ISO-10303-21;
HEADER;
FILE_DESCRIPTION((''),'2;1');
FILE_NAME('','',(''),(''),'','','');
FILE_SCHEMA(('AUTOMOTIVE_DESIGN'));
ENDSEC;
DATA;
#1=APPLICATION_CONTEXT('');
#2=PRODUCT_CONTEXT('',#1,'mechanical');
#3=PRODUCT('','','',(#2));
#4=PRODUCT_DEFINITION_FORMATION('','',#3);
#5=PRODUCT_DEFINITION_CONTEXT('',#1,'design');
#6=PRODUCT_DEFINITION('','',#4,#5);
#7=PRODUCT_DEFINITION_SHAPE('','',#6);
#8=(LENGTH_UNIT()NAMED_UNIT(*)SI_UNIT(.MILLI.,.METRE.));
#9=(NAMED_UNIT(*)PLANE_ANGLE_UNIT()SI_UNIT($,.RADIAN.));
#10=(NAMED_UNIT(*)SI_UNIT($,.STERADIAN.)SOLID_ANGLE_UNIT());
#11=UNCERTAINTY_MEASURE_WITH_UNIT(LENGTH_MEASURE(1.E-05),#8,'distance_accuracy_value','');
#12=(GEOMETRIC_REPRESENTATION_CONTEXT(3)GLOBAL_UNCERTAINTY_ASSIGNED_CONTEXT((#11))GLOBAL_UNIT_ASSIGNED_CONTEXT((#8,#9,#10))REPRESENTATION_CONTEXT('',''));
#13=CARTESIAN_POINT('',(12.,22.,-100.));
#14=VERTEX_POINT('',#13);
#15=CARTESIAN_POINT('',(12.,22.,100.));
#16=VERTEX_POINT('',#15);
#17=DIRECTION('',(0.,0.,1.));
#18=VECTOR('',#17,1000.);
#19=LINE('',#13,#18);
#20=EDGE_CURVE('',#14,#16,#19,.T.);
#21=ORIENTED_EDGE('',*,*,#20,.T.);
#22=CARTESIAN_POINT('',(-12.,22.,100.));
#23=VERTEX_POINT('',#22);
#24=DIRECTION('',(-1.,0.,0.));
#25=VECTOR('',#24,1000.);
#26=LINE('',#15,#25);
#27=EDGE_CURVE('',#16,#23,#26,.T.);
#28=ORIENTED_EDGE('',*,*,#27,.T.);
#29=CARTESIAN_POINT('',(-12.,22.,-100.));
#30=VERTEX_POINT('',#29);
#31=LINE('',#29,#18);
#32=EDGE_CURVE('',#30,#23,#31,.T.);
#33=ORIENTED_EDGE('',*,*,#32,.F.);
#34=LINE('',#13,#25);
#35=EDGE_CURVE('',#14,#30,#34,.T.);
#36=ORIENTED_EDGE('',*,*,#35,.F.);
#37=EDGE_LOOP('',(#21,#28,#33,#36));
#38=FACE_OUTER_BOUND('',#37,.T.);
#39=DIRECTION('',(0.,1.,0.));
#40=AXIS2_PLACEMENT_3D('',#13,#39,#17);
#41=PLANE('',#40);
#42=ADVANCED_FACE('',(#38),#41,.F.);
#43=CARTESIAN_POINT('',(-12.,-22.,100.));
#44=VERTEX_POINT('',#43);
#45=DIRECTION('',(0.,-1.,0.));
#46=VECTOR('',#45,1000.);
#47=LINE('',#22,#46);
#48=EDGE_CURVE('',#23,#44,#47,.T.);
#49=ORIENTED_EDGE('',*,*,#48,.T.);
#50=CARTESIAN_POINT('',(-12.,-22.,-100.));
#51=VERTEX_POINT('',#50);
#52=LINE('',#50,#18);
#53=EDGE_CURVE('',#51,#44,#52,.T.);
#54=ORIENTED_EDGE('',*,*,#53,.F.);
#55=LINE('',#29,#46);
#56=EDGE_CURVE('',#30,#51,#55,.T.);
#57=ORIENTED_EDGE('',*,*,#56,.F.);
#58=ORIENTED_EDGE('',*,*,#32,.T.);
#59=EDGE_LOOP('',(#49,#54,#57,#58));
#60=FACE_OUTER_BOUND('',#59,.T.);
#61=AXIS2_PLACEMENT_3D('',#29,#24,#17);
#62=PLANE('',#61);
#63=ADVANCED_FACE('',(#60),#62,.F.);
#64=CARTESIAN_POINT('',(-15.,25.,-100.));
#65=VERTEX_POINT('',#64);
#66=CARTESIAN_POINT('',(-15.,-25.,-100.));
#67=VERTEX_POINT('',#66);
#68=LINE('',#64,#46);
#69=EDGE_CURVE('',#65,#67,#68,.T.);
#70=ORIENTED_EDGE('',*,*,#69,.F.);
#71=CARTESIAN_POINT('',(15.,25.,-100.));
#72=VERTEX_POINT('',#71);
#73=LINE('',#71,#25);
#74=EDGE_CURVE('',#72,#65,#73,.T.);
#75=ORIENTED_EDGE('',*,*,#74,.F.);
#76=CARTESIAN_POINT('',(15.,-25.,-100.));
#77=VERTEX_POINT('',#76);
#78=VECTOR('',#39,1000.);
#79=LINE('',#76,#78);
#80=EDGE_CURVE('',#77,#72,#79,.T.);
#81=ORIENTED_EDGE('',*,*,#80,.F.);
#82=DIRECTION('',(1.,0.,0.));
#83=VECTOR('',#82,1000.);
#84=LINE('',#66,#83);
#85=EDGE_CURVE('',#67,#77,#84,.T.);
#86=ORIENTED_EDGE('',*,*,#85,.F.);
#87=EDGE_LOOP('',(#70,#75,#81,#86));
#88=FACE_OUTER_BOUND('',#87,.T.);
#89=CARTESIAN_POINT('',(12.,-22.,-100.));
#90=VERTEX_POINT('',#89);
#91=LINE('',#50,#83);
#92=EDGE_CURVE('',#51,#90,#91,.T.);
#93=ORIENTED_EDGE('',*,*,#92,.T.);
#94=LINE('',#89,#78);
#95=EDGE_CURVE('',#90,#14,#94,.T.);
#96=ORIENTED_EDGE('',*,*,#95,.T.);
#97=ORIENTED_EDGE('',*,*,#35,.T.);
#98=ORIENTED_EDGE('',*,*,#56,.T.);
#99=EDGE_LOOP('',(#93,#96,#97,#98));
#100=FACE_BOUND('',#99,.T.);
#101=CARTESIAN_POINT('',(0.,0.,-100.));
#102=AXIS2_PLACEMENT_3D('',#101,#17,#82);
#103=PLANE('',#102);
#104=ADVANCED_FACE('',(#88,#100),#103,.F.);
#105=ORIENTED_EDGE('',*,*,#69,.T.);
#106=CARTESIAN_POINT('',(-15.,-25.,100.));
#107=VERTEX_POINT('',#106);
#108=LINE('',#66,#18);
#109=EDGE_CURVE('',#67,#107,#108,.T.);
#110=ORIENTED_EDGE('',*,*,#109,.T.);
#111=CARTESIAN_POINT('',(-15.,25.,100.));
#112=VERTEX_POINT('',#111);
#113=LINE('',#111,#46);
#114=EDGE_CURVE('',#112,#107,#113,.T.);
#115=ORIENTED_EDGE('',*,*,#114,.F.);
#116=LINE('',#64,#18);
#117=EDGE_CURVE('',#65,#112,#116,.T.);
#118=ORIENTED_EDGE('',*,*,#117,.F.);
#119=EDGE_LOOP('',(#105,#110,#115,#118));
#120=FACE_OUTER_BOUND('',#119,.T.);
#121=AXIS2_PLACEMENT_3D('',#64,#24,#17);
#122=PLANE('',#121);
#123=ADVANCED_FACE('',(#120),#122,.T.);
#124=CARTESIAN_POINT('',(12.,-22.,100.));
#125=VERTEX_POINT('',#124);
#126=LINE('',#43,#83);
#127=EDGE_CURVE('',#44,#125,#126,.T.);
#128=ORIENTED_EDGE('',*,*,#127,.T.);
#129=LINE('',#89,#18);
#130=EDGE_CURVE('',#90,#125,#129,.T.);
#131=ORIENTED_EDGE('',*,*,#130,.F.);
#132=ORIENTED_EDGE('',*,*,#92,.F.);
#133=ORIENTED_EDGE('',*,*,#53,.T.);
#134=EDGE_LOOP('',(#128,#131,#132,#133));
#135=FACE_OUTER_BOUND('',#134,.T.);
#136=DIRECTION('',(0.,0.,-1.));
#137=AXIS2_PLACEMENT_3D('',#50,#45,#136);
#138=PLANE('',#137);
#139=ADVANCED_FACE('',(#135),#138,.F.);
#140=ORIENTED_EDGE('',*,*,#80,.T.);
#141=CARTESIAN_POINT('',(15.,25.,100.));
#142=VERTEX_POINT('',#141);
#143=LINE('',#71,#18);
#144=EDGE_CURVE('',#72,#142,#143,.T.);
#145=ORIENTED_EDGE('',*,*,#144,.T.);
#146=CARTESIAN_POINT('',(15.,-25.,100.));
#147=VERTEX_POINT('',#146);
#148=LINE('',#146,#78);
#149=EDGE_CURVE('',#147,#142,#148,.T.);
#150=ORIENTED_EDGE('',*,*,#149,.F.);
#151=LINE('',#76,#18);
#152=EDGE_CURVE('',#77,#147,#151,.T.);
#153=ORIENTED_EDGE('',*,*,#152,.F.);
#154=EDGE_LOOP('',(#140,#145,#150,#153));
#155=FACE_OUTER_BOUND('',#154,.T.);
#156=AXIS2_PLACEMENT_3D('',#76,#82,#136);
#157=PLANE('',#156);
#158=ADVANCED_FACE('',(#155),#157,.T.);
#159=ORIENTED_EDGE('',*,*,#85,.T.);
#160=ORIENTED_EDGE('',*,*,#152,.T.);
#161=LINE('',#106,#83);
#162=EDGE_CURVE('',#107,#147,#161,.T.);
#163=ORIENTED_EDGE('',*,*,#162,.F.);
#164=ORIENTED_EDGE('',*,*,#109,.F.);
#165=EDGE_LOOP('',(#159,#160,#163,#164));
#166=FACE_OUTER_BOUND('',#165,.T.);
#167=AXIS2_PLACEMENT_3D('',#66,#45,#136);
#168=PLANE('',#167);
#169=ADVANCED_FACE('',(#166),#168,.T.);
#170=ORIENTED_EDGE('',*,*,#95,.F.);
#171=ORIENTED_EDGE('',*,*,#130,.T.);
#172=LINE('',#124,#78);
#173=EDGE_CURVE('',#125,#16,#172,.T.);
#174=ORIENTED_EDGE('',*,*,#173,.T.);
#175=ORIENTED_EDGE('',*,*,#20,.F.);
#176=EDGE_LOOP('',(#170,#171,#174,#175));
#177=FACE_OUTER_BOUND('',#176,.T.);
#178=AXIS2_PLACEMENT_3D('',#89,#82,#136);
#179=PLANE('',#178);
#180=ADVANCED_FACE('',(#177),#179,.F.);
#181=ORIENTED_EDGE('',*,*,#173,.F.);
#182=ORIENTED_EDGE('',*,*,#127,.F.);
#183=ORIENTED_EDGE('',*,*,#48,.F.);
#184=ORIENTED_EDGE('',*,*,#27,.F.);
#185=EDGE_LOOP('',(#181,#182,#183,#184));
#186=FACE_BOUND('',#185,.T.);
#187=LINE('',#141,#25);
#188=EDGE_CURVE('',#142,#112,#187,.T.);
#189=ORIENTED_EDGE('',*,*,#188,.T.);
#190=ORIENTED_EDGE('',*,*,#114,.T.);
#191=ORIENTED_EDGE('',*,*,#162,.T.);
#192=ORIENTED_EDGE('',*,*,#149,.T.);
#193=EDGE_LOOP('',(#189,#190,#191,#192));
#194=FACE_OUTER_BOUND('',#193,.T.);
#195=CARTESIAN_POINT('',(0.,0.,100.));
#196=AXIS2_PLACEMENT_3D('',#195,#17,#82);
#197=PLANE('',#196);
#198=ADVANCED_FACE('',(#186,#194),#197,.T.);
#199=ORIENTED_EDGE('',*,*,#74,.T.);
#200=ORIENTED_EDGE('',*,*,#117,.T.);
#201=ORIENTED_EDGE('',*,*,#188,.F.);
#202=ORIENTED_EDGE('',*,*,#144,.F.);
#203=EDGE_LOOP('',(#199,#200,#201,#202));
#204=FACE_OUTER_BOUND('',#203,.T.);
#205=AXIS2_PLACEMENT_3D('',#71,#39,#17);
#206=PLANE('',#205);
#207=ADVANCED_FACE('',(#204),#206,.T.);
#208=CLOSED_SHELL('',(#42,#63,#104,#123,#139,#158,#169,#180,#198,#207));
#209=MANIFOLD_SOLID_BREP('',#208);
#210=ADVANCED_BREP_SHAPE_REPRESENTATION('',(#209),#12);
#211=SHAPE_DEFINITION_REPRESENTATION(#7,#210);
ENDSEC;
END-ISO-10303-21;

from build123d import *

# Parameters (mm, degrees)
SKETCH_1_W      = 30
SKETCH_1_H      = 50
SKETCH_1_W_2    = 24
SKETCH_1_H_2    = 44
EXTRUDE_1_DEPTH = 100


with BuildPart() as part:
    # 草图1 → 凸台-拉伸1 (new, symmetric)
    with BuildSketch(Plane.XY):
        Rectangle(SKETCH_1_W, SKETCH_1_H)
        Rectangle(SKETCH_1_W_2, SKETCH_1_H_2, mode=Mode.SUBTRACT)
    extrude(amount=EXTRUDE_1_DEPTH, both=True)


solid = part.part
